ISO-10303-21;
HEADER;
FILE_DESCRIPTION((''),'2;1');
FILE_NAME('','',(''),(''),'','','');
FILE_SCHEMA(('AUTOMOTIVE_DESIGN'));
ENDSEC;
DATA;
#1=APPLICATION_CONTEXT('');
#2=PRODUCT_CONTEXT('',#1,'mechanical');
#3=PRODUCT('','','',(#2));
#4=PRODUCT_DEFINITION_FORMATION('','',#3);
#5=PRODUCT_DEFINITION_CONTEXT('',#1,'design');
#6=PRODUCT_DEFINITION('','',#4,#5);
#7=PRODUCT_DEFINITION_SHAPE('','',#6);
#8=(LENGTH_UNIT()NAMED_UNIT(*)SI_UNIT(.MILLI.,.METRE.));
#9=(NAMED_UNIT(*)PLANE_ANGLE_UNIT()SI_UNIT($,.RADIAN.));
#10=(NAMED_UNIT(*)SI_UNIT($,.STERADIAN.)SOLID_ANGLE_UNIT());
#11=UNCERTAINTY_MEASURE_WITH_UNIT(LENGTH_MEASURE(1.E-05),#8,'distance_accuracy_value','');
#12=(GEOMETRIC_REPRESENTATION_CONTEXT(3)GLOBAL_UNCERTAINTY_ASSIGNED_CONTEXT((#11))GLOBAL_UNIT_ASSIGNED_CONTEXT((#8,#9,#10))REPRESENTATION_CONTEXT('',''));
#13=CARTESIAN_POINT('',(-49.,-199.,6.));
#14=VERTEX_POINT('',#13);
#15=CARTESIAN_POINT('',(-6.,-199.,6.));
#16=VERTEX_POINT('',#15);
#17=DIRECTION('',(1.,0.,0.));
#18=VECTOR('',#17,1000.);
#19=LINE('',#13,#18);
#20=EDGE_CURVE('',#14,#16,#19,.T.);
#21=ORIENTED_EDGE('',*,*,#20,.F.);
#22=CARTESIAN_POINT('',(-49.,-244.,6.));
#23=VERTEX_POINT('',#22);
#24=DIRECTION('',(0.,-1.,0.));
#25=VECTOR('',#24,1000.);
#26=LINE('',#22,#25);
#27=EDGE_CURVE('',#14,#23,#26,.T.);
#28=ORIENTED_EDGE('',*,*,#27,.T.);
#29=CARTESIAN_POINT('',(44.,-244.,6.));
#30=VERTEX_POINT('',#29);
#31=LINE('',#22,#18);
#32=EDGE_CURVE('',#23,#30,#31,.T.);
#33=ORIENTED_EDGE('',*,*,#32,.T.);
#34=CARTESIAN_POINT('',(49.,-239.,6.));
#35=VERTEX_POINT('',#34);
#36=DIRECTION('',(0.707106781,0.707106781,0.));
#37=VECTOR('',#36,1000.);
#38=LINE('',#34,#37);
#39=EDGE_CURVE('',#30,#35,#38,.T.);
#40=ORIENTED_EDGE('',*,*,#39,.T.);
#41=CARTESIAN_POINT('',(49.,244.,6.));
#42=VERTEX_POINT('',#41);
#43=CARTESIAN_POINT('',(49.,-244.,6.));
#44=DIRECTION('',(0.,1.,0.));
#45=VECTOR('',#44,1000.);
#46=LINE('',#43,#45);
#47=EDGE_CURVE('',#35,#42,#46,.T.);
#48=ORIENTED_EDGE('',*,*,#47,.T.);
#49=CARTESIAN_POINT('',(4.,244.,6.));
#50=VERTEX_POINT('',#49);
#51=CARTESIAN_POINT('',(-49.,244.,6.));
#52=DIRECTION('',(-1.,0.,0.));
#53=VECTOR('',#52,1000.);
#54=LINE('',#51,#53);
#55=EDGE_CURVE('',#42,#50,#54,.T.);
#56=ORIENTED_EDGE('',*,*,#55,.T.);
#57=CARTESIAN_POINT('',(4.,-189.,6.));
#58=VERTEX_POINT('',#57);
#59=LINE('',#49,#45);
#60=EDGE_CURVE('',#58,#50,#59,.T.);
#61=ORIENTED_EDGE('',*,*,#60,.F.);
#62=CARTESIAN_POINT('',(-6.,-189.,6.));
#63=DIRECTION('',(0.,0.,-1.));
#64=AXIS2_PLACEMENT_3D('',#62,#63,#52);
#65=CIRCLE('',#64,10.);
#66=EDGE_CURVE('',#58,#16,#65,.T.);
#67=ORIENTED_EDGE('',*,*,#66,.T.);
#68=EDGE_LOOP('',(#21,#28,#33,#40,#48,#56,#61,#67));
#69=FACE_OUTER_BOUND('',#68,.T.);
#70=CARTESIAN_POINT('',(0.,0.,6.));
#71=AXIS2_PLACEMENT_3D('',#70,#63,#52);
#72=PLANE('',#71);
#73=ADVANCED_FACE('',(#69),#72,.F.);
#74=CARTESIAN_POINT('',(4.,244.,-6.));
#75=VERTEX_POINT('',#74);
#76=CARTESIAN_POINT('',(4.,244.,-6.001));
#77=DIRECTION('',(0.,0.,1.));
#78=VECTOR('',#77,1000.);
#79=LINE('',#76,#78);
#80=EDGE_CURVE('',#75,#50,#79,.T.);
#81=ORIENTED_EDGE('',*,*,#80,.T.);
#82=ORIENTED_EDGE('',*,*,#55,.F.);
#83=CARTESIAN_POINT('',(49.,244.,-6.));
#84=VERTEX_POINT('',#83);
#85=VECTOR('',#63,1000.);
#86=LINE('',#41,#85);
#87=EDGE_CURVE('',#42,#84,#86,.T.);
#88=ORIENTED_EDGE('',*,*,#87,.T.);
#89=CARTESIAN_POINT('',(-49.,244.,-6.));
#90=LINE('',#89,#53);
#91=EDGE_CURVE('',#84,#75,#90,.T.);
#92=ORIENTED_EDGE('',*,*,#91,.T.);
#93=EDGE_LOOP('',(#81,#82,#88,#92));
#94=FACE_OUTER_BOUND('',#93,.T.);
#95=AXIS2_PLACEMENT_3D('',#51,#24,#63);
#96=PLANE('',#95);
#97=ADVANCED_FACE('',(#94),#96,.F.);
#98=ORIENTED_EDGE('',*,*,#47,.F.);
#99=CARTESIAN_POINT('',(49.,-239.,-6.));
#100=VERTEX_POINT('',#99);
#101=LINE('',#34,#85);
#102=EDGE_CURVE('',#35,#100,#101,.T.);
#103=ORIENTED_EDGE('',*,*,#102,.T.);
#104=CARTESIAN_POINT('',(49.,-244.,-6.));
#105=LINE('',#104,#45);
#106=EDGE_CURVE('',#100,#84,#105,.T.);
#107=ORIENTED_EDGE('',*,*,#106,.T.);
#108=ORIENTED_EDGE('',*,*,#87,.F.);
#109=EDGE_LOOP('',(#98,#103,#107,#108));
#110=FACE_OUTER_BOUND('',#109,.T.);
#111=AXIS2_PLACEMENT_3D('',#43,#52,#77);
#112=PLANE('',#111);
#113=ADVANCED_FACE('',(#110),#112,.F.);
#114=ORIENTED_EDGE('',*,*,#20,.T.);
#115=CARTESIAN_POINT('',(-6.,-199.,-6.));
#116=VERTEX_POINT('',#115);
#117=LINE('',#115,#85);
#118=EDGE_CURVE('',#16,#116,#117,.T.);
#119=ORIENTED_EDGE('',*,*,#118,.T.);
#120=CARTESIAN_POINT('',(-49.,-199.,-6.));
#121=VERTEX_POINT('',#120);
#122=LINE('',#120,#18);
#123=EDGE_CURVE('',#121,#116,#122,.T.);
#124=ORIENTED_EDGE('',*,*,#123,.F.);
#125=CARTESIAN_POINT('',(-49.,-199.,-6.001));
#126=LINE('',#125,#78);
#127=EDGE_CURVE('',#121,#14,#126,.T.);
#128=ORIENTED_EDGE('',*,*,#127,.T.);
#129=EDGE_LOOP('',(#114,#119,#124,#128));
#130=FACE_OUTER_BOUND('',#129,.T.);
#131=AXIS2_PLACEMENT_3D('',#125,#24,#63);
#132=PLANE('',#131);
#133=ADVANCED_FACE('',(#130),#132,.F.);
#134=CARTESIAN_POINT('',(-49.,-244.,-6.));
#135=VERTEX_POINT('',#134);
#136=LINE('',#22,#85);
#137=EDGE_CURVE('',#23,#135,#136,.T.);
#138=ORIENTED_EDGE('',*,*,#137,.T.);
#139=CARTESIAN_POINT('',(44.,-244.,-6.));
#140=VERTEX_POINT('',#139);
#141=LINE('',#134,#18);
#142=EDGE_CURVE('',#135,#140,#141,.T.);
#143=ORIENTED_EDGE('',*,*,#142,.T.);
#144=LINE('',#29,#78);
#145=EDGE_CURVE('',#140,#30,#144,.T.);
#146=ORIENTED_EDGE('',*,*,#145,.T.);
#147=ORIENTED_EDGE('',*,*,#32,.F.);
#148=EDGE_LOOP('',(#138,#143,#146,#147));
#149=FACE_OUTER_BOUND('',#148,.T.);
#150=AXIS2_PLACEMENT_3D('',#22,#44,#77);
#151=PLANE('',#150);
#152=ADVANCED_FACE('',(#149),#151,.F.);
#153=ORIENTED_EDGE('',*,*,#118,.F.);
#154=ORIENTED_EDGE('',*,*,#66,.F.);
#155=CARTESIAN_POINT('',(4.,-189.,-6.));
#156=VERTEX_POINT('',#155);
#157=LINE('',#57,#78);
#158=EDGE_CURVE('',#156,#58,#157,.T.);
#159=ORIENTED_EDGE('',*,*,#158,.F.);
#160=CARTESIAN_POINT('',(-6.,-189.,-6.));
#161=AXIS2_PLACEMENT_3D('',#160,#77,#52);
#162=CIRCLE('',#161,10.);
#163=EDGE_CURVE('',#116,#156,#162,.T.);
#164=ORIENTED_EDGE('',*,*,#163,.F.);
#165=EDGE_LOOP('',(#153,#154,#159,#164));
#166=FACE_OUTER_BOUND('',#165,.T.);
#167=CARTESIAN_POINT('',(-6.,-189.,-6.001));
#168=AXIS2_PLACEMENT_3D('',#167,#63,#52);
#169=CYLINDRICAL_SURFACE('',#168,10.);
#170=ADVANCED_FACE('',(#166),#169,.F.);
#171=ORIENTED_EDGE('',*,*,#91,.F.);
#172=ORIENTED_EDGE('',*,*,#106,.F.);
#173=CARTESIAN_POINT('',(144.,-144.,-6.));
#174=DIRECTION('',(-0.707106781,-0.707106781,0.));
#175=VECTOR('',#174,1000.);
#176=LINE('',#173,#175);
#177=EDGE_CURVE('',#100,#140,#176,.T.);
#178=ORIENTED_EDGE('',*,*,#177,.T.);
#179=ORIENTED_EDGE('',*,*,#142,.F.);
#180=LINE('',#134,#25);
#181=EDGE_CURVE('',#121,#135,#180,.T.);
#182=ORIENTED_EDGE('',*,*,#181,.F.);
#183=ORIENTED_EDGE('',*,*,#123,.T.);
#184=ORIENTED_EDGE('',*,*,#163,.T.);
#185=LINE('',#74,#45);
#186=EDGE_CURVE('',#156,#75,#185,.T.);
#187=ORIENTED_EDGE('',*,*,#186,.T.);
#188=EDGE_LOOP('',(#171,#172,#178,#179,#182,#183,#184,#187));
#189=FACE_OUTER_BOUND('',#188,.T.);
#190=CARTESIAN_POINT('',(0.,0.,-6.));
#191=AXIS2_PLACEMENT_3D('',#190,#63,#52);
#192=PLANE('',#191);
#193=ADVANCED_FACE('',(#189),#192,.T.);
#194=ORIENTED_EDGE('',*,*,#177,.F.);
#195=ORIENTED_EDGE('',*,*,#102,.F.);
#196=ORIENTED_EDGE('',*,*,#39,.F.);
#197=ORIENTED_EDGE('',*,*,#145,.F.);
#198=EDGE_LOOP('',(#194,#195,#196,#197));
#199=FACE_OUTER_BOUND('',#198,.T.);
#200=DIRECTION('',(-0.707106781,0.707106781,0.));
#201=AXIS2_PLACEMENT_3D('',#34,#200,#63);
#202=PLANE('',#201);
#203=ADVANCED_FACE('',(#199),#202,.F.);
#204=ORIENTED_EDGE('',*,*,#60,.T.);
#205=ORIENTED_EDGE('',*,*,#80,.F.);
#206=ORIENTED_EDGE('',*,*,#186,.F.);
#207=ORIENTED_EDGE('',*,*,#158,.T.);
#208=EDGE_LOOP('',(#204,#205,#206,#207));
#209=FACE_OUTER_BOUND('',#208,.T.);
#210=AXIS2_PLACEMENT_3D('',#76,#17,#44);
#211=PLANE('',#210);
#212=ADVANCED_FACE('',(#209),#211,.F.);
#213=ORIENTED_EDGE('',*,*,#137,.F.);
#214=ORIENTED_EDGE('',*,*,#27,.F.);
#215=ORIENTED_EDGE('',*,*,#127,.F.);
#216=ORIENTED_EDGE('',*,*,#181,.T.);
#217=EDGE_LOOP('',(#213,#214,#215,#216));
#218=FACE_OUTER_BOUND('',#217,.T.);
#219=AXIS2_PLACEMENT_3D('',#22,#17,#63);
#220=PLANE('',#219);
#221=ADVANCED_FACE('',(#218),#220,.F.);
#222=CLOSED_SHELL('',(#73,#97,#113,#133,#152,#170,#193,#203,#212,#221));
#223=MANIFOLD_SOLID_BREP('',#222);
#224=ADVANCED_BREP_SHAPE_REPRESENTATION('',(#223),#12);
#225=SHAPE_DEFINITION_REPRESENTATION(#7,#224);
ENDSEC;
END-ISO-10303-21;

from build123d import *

# Parameters (mm, degrees)
SKETCH_1_W          = 98
SKETCH_1_H          = 488
EXTRUDE_1_DEPTH     = 6
CUT_EXTRUDE_1_REACH = 251.161
SKETCH_2_W          = 53
SKETCH_2_H          = 443
FILLET_1_R          = 10
CHAMFER_1_SIZE      = 5


with BuildPart() as part:
    # 草图1 → 凸台-拉伸1 (new, symmetric)
    with BuildSketch(Plane.XY):
        Rectangle(SKETCH_1_W, SKETCH_1_H)
    extrude(amount=EXTRUDE_1_DEPTH, both=True)

    # 草图2 → 切除-拉伸1 (cut, up to next)
    with BuildSketch(Plane.XY.offset(6), mode=Mode.PRIVATE) as cut_extrude_1_sk1:
        with Locations((-22.5, 22.5)):
            Rectangle(SKETCH_2_W, SKETCH_2_H)
    cut_extrude_1_tool1 = extrude(cut_extrude_1_sk1.sketch, amount=-CUT_EXTRUDE_1_REACH, mode=Mode.PRIVATE) & part.part
    add(cut_extrude_1_tool1.solids().sort_by_distance((-22.5, 22.5, 6))[0], mode=Mode.SUBTRACT)

    # 圆角1
    fillet_1_edges = [part.edges().sort_by_distance(p)[0] for p in [
        (4, -199, 0),
    ]]
    fillet(fillet_1_edges, radius=FILLET_1_R)

    # 倒角1
    chamfer_1_edges = [part.edges().sort_by_distance(p)[0] for p in [
        (49, -244, 0),
    ]]
    chamfer(chamfer_1_edges, length=CHAMFER_1_SIZE)


solid = part.part
